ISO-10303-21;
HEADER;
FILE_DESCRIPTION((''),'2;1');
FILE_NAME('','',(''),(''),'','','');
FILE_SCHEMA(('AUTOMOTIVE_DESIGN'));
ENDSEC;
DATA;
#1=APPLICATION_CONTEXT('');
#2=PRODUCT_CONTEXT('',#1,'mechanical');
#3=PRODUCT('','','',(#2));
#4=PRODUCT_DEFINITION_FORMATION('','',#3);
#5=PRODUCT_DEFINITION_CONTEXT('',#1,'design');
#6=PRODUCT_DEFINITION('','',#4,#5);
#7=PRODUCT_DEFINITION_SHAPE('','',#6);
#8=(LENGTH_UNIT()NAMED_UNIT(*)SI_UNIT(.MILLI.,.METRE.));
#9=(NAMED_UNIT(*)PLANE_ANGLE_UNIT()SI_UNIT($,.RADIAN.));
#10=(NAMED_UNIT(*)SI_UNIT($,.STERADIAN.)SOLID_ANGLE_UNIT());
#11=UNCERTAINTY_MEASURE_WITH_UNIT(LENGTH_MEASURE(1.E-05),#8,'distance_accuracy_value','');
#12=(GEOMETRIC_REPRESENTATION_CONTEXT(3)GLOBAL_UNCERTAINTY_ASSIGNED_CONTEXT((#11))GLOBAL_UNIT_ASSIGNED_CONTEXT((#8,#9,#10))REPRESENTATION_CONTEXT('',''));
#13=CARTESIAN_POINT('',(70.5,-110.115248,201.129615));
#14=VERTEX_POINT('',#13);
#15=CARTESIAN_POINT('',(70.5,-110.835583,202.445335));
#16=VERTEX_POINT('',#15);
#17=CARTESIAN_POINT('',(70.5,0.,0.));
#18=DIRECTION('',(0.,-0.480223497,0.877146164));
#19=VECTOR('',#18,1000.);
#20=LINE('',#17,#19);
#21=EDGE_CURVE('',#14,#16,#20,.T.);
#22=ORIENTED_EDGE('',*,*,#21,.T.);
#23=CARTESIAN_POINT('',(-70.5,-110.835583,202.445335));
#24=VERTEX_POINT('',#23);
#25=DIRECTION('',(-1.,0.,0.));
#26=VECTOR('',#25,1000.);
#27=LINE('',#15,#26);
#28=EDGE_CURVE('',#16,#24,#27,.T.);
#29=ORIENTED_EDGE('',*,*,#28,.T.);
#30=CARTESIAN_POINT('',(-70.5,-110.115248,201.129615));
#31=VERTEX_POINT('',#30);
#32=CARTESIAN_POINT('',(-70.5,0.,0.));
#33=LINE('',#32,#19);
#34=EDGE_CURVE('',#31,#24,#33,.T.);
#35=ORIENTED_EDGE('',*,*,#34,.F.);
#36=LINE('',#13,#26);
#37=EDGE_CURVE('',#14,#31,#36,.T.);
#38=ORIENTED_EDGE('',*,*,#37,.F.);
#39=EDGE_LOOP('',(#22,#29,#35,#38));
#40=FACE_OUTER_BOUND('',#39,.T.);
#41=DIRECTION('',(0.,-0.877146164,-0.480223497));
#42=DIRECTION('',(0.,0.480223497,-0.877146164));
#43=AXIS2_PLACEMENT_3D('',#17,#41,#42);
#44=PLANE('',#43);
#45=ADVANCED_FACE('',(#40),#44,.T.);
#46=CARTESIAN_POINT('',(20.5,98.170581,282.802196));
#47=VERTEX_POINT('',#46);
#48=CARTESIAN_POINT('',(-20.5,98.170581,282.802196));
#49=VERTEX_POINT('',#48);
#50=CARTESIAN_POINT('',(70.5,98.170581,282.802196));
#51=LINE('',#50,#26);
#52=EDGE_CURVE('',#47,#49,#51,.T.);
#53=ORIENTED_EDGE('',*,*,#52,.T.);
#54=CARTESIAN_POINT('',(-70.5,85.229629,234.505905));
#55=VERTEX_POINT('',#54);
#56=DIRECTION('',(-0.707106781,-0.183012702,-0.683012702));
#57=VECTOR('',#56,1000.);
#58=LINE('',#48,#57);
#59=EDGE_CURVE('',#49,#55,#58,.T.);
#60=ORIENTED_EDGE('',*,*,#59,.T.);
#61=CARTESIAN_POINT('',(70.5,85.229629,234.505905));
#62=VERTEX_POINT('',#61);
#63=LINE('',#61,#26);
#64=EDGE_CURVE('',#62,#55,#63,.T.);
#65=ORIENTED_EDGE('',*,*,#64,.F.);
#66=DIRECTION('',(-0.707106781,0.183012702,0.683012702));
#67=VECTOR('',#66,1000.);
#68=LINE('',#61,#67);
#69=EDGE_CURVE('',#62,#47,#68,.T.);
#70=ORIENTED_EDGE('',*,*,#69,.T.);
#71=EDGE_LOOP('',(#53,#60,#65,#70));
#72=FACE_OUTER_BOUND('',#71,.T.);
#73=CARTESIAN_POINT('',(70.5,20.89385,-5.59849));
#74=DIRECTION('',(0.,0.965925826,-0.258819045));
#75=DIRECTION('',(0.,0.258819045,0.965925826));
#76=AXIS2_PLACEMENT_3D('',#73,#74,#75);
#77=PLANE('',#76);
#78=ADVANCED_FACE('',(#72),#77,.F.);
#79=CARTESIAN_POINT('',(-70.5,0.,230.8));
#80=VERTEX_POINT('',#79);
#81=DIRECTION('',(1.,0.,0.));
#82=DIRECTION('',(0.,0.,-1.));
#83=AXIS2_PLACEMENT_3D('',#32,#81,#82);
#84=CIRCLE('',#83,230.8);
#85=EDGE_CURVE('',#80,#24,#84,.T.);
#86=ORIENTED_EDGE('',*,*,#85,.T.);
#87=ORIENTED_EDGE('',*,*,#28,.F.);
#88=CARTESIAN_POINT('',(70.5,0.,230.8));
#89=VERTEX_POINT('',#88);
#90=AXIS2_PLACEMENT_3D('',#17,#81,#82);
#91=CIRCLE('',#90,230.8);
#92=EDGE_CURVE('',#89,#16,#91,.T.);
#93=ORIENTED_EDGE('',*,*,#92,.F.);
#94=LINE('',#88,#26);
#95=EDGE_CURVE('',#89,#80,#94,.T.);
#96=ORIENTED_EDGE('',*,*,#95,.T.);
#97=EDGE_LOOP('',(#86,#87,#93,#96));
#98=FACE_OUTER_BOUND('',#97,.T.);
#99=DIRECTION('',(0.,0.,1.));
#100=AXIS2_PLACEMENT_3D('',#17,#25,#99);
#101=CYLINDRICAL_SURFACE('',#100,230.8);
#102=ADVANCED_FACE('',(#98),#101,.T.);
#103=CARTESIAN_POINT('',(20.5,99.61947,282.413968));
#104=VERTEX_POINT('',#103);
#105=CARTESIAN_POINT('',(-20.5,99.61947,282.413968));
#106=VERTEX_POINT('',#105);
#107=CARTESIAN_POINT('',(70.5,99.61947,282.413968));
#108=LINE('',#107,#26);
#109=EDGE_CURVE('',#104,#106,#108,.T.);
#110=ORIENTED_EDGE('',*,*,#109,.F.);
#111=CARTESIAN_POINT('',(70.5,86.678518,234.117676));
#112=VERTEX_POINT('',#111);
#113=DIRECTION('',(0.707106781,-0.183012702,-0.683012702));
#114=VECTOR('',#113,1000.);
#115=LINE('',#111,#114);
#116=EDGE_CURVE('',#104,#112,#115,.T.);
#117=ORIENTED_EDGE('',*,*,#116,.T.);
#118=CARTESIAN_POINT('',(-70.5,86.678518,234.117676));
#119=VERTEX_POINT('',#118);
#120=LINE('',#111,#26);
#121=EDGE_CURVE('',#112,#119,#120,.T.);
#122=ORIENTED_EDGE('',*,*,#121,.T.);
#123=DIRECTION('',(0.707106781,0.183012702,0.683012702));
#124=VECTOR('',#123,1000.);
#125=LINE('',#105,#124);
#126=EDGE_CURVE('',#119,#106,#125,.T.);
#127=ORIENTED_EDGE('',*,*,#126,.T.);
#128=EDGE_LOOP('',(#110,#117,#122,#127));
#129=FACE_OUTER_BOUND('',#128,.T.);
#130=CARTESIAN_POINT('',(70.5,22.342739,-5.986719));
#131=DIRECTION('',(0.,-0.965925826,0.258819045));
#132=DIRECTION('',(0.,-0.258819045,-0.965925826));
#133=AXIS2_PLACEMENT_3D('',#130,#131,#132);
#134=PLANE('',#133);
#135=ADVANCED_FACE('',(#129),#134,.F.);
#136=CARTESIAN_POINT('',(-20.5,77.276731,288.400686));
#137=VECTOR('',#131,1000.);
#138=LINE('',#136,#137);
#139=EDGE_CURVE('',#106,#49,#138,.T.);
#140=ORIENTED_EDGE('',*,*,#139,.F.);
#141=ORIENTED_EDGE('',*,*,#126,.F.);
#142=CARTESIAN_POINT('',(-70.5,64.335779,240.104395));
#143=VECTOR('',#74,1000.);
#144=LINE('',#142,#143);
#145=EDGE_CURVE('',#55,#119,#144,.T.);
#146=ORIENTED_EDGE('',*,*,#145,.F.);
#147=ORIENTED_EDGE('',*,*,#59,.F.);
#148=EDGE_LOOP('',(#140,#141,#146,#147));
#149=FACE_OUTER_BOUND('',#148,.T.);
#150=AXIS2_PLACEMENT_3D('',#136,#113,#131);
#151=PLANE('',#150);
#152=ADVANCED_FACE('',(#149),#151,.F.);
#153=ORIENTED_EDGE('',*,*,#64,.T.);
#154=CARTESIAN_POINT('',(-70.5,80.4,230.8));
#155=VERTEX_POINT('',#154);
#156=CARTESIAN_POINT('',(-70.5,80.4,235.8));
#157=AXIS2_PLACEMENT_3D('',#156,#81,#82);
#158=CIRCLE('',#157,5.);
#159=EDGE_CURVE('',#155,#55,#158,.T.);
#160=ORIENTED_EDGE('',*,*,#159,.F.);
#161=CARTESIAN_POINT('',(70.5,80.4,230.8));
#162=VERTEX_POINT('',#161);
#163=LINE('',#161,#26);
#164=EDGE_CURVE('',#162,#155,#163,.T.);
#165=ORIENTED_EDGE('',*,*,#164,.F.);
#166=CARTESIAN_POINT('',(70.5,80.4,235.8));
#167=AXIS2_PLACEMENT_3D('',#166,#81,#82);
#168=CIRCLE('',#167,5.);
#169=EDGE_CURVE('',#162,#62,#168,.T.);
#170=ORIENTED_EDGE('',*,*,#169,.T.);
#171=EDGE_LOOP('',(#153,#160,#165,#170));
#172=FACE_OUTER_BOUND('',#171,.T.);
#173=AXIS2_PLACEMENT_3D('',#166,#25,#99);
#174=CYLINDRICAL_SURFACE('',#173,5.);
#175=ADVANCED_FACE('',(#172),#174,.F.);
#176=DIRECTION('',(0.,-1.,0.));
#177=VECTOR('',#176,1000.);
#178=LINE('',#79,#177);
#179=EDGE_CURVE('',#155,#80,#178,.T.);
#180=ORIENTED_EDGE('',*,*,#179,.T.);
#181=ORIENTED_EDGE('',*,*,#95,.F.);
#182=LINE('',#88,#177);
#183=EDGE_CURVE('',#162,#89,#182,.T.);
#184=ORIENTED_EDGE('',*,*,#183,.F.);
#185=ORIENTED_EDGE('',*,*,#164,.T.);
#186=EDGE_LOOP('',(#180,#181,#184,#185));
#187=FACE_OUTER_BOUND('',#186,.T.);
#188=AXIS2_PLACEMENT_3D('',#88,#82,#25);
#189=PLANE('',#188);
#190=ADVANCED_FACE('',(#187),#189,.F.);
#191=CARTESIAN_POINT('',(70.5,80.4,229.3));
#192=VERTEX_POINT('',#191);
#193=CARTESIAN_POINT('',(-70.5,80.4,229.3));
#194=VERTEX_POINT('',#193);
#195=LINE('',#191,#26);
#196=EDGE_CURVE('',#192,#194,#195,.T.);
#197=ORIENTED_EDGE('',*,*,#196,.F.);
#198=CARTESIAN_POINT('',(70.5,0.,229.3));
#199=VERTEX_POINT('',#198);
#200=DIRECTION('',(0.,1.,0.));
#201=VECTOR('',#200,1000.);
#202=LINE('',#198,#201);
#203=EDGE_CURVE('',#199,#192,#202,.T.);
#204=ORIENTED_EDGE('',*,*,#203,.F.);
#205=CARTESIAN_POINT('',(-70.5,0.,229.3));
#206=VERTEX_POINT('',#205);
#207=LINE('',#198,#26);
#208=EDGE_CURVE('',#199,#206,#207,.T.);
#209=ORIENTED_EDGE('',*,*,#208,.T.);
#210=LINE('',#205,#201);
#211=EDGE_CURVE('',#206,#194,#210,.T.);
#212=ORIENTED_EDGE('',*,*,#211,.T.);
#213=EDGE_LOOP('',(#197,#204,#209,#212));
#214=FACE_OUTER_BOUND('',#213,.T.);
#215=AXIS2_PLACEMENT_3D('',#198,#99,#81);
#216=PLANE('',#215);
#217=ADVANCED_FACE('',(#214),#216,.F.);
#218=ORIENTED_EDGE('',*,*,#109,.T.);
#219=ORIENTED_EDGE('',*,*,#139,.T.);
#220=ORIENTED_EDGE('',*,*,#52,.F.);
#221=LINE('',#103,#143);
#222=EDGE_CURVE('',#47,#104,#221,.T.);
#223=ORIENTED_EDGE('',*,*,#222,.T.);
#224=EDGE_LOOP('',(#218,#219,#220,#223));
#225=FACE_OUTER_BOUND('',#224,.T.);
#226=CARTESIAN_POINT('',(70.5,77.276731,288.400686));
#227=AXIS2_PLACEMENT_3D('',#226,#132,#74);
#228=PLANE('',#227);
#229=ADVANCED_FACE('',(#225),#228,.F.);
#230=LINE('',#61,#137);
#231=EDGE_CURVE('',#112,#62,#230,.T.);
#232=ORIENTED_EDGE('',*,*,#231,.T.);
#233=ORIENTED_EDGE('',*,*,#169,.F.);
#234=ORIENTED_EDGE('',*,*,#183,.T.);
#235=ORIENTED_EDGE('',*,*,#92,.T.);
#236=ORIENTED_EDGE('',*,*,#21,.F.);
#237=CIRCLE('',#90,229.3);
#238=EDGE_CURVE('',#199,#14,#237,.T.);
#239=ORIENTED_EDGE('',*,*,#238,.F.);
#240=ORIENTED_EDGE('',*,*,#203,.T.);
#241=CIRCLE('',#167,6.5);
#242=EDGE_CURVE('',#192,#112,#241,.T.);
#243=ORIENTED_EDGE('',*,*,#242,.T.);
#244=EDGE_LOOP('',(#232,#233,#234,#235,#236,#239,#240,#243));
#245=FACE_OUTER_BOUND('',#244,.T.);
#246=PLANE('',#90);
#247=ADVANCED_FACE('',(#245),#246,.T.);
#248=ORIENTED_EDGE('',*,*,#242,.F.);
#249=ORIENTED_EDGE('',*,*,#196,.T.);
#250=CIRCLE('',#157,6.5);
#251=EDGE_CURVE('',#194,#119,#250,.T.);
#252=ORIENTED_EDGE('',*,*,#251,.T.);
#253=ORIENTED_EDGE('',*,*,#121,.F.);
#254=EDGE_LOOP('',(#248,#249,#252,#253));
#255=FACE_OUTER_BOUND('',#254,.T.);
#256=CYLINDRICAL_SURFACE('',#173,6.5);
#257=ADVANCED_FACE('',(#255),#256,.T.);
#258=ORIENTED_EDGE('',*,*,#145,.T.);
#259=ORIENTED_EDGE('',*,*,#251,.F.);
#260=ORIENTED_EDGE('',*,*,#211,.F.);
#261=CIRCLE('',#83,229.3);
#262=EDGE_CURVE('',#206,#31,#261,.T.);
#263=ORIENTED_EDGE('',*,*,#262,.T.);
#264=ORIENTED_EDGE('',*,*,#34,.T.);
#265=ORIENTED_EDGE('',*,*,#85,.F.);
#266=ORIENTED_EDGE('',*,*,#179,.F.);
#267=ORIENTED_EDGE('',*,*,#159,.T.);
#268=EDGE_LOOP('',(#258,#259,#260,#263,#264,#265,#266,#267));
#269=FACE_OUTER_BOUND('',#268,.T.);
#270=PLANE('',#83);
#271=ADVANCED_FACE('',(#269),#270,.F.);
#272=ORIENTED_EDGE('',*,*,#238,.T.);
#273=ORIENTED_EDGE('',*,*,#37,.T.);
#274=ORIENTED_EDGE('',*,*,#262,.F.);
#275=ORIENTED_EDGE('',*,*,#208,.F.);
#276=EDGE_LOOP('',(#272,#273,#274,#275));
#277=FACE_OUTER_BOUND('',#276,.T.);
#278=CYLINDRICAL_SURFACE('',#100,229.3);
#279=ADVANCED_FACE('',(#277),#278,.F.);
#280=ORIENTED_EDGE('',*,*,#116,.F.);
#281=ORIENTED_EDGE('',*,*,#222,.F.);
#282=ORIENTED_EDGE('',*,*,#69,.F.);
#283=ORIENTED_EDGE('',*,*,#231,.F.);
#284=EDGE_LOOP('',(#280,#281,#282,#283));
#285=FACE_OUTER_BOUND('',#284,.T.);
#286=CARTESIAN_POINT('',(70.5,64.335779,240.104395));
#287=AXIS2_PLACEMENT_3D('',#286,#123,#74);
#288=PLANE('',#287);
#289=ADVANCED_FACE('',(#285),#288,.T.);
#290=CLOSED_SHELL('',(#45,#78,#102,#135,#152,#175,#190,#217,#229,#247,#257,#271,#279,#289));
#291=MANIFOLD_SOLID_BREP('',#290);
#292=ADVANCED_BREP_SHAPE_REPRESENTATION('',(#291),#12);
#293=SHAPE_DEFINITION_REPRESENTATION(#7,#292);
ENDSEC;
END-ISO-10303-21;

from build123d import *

# Parameters (mm, degrees)
BOSS_EXTRUDE1_DEPTH = 70.5
CHAMFER1_SIZE       = 50


with BuildPart() as part:
    # Sketch1 → Boss-Extrude1 (new, symmetric)
    with BuildSketch(Plane(origin=(0, 0, 0), x_dir=(0, 0, -1), z_dir=(1, 0, 0))):
        with BuildLine():
            ThreePointArc((-230.8, 80.4), (-231.833233299, 83.443807145), (-234.505904774, 85.229629131))
            Line((-234.505904774, 85.229629131), (-282.802196089, 98.170581387))
            Line((-282.802196089, 98.170581387), (-282.413967521, 99.619470126))
            Line((-282.413967521, 99.619470126), (-234.117676207, 86.678517871))
            ThreePointArc((-234.117676207, 86.678517871), (-230.643203288, 84.356949289), (-229.3, 80.4))
            Line((-229.3, 80.4), (-229.3, 0))
            ThreePointArc((-229.3, 0), (-222.145797616, -56.830754012), (-201.129615338, -110.115247964))
            Line((-201.129615338, -110.115247964), (-202.445334583, -110.83558321))
            ThreePointArc((-202.445334583, -110.83558321), (-223.598997339, -57.202520828), (-230.8, 0))
            Line((-230.8, 0), (-230.8, 80.4))
        make_face()
    extrude(amount=BOSS_EXTRUDE1_DEPTH, both=True)

    # Chamfer1
    chamfer1_edges = [part.edges().sort_by_distance(p)[0] for p in [
        (-70.5, 98.895025756, 282.608081805),
        (70.5, 98.895025756, 282.608081805),
    ]]
    chamfer(chamfer1_edges, length=CHAMFER1_SIZE)


solid = part.part
